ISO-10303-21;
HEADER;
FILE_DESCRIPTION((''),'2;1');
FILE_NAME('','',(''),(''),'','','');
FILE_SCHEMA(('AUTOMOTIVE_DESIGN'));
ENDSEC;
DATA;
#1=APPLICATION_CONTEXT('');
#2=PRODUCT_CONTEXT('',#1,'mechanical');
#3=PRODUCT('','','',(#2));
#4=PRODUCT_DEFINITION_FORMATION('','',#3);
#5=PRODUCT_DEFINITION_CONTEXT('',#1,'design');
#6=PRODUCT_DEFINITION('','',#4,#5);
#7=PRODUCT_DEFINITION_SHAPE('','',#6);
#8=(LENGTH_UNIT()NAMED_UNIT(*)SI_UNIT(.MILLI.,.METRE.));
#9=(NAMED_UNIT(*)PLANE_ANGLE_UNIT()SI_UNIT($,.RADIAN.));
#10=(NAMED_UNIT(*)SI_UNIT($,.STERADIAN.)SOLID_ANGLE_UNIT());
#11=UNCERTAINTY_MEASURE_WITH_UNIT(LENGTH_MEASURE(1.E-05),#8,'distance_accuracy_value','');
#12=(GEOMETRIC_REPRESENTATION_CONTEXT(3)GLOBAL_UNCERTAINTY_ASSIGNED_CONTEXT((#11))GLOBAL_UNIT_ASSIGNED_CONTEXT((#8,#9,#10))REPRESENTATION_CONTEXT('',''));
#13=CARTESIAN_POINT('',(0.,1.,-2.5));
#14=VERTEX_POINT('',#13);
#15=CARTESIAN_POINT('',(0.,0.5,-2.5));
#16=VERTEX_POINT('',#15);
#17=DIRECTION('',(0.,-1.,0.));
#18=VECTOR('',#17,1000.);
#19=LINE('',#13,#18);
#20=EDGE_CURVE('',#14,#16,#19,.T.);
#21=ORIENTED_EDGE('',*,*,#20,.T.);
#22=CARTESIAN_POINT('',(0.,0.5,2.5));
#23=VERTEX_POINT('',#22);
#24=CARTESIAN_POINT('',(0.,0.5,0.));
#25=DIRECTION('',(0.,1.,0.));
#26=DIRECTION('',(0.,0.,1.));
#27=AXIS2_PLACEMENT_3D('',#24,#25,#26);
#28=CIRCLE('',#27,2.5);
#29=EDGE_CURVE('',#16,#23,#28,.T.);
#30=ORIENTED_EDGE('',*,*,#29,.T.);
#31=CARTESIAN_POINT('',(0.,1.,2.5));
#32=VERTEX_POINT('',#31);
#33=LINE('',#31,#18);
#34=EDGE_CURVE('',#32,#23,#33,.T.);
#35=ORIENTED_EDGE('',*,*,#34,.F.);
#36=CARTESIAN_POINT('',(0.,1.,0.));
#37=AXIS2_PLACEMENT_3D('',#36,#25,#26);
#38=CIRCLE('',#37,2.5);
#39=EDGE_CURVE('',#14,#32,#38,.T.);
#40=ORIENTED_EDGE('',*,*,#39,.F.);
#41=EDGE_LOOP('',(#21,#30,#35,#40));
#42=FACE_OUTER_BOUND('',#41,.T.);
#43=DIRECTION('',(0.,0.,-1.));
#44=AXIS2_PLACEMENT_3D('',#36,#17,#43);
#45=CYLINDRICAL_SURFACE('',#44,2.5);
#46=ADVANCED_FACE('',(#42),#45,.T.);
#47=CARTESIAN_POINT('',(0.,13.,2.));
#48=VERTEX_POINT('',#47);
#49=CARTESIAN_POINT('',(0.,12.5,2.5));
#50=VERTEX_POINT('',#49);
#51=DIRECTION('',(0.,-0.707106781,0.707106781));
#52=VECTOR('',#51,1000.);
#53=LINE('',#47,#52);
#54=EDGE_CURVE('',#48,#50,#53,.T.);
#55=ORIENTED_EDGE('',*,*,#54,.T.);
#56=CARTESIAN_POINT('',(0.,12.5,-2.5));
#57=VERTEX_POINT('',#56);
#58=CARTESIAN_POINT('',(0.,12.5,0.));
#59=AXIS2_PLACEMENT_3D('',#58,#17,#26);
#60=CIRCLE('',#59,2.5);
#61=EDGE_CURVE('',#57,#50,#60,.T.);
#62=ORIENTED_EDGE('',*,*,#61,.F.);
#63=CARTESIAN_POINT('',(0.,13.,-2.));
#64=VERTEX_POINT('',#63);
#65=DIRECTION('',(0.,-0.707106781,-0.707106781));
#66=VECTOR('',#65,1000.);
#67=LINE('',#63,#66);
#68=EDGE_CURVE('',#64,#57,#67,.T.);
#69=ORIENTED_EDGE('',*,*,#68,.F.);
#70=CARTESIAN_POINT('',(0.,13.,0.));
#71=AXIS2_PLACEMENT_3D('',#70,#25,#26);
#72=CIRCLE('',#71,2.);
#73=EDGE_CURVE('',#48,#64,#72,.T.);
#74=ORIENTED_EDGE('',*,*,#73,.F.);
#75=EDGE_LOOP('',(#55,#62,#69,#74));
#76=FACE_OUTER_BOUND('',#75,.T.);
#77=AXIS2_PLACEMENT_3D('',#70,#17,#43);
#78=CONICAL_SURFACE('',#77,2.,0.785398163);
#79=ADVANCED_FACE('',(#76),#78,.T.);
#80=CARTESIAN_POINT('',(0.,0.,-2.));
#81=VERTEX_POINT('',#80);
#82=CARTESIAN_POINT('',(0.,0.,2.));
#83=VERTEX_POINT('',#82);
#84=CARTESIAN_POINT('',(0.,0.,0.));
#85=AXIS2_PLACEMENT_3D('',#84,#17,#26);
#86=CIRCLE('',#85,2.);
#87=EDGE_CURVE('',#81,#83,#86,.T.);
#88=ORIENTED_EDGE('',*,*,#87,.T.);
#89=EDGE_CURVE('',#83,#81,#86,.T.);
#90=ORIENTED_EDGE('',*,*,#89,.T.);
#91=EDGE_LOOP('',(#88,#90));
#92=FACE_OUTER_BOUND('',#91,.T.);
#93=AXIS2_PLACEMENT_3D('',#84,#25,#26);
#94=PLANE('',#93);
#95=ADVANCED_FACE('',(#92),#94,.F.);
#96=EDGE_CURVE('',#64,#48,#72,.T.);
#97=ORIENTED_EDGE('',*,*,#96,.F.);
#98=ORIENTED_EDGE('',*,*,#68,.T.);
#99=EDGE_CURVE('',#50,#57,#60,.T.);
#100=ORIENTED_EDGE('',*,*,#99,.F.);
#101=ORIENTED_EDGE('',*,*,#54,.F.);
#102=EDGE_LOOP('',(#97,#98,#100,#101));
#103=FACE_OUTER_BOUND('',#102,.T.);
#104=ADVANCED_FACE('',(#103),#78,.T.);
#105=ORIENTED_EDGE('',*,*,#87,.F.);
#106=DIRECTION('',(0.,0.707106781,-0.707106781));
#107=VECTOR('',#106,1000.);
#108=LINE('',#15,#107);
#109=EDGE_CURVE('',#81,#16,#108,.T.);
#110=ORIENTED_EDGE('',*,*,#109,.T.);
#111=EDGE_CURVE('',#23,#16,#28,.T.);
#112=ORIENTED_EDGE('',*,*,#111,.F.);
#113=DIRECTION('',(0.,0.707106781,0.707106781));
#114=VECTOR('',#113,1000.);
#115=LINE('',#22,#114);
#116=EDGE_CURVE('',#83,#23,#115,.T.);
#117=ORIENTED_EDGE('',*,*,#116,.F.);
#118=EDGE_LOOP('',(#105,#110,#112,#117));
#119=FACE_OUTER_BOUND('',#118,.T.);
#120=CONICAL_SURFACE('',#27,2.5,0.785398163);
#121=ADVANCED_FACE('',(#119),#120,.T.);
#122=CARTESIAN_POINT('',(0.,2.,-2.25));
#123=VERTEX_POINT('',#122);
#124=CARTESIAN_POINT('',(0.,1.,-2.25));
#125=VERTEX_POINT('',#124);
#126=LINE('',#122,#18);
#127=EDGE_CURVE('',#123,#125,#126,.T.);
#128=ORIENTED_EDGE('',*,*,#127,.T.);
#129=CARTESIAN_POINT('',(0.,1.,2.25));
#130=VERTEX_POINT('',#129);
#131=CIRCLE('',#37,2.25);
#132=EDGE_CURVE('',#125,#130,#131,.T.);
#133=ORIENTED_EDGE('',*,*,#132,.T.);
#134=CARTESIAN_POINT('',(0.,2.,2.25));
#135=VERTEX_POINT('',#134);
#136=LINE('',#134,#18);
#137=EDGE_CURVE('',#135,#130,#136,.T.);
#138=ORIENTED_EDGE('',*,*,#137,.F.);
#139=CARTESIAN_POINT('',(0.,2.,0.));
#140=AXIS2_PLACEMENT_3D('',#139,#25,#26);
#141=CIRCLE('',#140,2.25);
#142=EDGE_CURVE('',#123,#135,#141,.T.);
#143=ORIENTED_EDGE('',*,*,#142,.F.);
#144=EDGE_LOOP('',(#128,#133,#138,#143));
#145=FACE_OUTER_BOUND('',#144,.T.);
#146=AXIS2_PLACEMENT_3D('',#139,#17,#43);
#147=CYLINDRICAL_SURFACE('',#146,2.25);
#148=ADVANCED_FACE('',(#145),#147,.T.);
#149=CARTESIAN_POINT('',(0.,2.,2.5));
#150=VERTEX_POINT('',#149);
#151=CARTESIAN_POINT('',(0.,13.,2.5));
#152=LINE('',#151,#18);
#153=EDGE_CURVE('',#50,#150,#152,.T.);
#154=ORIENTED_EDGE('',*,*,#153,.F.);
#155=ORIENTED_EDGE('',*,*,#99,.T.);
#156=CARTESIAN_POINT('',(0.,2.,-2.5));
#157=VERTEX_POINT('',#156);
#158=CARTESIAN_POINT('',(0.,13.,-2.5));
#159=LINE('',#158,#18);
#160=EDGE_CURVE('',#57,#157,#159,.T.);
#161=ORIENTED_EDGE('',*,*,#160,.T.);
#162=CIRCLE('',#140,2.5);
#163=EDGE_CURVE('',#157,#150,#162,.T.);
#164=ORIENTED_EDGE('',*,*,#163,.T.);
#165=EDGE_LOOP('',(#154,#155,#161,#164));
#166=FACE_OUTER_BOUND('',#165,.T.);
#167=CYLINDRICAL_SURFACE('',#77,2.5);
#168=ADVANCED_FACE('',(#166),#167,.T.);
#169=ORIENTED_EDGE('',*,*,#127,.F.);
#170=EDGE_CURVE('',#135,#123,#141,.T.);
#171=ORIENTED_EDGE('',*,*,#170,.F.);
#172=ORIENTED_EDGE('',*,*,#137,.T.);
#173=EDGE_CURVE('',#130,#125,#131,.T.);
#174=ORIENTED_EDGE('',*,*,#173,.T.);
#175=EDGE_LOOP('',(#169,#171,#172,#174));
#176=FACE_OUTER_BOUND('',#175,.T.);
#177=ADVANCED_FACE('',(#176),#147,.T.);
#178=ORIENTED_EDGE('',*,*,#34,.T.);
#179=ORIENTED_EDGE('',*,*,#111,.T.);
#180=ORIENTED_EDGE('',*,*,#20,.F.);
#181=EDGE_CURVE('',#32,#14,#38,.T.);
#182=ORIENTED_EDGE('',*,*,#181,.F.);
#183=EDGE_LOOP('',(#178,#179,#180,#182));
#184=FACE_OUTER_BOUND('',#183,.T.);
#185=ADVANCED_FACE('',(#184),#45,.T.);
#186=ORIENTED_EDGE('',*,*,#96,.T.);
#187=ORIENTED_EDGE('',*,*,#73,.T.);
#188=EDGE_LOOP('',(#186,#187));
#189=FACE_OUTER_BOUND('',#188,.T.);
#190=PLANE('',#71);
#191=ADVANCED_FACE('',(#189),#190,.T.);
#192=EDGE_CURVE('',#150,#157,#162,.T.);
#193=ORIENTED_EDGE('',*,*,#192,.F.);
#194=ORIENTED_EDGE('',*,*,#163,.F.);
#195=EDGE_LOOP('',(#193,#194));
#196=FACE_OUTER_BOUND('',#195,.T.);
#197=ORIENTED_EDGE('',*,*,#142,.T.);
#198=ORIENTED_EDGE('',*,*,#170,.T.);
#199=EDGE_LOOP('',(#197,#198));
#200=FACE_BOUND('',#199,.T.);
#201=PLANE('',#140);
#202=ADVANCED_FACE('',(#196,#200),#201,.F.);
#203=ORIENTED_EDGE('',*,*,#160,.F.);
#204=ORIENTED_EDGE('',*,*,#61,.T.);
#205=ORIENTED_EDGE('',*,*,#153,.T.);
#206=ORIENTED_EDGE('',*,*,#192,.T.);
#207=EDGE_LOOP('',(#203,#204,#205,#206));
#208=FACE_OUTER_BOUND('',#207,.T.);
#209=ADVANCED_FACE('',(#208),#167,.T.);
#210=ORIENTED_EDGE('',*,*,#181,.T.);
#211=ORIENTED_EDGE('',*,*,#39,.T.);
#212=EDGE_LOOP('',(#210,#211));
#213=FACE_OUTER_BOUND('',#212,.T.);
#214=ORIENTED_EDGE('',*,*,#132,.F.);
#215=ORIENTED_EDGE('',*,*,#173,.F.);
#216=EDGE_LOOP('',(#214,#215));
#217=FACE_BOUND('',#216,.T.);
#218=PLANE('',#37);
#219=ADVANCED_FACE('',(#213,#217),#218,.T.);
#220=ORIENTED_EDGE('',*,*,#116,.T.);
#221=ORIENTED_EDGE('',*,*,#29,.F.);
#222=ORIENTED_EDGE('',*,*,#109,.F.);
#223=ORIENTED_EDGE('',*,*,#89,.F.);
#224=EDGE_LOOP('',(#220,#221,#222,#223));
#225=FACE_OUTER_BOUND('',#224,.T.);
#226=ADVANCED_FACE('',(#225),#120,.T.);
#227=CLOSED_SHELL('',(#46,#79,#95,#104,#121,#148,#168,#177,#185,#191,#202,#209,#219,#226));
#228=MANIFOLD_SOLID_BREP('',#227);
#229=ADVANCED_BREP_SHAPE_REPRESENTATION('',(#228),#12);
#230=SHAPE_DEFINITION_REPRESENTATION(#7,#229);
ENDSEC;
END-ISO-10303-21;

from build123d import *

# Parameters (mm, degrees)
SKETCH1_R           = 2.5
BOSS_EXTRUDE1_DEPTH = 1
SKETCH2_R           = 2.25
BOSS_EXTRUDE2_DEPTH = 1
SKETCH3_R           = 2.5
BOSS_EXTRUDE3_DEPTH = 11
CHAMFER1_SIZE       = 0.5


with BuildPart() as part:
    # Sketch1 → Boss-Extrude1 (new body)
    with BuildSketch(Plane(origin=(0, 0, 0), x_dir=(1, 0, 0), z_dir=(0, 1, 0))):
        with Locations(Location((0, 0, 0), (0, 0, 270))):
            Circle(SKETCH1_R)
    extrude(amount=BOSS_EXTRUDE1_DEPTH)

    # Sketch2 → Boss-Extrude2 (add)
    with BuildSketch(Plane(origin=(0, 1, 0), x_dir=(1, 0, 0), z_dir=(0, 1, 0))):
        with Locations(Location((0, 0, 0), (0, 0, 270))):
            Circle(SKETCH2_R)
    extrude(amount=BOSS_EXTRUDE2_DEPTH)

    # Sketch3 → Boss-Extrude3 (add)
    with BuildSketch(Plane(origin=(0, 2, 0), x_dir=(1, 0, 0), z_dir=(0, 1, 0))):
        with Locations(Location((0, 0, 0), (0, 0, 270))):
            Circle(SKETCH3_R)
    extrude(amount=BOSS_EXTRUDE3_DEPTH)

    # Chamfer1
    chamfer1_edges = [part.edges().sort_by_distance(p)[0] for p in [
        (0, 13, -2.5),
        (0, 0, -2.5),
    ]]
    chamfer(chamfer1_edges, length=CHAMFER1_SIZE)


solid = part.part
